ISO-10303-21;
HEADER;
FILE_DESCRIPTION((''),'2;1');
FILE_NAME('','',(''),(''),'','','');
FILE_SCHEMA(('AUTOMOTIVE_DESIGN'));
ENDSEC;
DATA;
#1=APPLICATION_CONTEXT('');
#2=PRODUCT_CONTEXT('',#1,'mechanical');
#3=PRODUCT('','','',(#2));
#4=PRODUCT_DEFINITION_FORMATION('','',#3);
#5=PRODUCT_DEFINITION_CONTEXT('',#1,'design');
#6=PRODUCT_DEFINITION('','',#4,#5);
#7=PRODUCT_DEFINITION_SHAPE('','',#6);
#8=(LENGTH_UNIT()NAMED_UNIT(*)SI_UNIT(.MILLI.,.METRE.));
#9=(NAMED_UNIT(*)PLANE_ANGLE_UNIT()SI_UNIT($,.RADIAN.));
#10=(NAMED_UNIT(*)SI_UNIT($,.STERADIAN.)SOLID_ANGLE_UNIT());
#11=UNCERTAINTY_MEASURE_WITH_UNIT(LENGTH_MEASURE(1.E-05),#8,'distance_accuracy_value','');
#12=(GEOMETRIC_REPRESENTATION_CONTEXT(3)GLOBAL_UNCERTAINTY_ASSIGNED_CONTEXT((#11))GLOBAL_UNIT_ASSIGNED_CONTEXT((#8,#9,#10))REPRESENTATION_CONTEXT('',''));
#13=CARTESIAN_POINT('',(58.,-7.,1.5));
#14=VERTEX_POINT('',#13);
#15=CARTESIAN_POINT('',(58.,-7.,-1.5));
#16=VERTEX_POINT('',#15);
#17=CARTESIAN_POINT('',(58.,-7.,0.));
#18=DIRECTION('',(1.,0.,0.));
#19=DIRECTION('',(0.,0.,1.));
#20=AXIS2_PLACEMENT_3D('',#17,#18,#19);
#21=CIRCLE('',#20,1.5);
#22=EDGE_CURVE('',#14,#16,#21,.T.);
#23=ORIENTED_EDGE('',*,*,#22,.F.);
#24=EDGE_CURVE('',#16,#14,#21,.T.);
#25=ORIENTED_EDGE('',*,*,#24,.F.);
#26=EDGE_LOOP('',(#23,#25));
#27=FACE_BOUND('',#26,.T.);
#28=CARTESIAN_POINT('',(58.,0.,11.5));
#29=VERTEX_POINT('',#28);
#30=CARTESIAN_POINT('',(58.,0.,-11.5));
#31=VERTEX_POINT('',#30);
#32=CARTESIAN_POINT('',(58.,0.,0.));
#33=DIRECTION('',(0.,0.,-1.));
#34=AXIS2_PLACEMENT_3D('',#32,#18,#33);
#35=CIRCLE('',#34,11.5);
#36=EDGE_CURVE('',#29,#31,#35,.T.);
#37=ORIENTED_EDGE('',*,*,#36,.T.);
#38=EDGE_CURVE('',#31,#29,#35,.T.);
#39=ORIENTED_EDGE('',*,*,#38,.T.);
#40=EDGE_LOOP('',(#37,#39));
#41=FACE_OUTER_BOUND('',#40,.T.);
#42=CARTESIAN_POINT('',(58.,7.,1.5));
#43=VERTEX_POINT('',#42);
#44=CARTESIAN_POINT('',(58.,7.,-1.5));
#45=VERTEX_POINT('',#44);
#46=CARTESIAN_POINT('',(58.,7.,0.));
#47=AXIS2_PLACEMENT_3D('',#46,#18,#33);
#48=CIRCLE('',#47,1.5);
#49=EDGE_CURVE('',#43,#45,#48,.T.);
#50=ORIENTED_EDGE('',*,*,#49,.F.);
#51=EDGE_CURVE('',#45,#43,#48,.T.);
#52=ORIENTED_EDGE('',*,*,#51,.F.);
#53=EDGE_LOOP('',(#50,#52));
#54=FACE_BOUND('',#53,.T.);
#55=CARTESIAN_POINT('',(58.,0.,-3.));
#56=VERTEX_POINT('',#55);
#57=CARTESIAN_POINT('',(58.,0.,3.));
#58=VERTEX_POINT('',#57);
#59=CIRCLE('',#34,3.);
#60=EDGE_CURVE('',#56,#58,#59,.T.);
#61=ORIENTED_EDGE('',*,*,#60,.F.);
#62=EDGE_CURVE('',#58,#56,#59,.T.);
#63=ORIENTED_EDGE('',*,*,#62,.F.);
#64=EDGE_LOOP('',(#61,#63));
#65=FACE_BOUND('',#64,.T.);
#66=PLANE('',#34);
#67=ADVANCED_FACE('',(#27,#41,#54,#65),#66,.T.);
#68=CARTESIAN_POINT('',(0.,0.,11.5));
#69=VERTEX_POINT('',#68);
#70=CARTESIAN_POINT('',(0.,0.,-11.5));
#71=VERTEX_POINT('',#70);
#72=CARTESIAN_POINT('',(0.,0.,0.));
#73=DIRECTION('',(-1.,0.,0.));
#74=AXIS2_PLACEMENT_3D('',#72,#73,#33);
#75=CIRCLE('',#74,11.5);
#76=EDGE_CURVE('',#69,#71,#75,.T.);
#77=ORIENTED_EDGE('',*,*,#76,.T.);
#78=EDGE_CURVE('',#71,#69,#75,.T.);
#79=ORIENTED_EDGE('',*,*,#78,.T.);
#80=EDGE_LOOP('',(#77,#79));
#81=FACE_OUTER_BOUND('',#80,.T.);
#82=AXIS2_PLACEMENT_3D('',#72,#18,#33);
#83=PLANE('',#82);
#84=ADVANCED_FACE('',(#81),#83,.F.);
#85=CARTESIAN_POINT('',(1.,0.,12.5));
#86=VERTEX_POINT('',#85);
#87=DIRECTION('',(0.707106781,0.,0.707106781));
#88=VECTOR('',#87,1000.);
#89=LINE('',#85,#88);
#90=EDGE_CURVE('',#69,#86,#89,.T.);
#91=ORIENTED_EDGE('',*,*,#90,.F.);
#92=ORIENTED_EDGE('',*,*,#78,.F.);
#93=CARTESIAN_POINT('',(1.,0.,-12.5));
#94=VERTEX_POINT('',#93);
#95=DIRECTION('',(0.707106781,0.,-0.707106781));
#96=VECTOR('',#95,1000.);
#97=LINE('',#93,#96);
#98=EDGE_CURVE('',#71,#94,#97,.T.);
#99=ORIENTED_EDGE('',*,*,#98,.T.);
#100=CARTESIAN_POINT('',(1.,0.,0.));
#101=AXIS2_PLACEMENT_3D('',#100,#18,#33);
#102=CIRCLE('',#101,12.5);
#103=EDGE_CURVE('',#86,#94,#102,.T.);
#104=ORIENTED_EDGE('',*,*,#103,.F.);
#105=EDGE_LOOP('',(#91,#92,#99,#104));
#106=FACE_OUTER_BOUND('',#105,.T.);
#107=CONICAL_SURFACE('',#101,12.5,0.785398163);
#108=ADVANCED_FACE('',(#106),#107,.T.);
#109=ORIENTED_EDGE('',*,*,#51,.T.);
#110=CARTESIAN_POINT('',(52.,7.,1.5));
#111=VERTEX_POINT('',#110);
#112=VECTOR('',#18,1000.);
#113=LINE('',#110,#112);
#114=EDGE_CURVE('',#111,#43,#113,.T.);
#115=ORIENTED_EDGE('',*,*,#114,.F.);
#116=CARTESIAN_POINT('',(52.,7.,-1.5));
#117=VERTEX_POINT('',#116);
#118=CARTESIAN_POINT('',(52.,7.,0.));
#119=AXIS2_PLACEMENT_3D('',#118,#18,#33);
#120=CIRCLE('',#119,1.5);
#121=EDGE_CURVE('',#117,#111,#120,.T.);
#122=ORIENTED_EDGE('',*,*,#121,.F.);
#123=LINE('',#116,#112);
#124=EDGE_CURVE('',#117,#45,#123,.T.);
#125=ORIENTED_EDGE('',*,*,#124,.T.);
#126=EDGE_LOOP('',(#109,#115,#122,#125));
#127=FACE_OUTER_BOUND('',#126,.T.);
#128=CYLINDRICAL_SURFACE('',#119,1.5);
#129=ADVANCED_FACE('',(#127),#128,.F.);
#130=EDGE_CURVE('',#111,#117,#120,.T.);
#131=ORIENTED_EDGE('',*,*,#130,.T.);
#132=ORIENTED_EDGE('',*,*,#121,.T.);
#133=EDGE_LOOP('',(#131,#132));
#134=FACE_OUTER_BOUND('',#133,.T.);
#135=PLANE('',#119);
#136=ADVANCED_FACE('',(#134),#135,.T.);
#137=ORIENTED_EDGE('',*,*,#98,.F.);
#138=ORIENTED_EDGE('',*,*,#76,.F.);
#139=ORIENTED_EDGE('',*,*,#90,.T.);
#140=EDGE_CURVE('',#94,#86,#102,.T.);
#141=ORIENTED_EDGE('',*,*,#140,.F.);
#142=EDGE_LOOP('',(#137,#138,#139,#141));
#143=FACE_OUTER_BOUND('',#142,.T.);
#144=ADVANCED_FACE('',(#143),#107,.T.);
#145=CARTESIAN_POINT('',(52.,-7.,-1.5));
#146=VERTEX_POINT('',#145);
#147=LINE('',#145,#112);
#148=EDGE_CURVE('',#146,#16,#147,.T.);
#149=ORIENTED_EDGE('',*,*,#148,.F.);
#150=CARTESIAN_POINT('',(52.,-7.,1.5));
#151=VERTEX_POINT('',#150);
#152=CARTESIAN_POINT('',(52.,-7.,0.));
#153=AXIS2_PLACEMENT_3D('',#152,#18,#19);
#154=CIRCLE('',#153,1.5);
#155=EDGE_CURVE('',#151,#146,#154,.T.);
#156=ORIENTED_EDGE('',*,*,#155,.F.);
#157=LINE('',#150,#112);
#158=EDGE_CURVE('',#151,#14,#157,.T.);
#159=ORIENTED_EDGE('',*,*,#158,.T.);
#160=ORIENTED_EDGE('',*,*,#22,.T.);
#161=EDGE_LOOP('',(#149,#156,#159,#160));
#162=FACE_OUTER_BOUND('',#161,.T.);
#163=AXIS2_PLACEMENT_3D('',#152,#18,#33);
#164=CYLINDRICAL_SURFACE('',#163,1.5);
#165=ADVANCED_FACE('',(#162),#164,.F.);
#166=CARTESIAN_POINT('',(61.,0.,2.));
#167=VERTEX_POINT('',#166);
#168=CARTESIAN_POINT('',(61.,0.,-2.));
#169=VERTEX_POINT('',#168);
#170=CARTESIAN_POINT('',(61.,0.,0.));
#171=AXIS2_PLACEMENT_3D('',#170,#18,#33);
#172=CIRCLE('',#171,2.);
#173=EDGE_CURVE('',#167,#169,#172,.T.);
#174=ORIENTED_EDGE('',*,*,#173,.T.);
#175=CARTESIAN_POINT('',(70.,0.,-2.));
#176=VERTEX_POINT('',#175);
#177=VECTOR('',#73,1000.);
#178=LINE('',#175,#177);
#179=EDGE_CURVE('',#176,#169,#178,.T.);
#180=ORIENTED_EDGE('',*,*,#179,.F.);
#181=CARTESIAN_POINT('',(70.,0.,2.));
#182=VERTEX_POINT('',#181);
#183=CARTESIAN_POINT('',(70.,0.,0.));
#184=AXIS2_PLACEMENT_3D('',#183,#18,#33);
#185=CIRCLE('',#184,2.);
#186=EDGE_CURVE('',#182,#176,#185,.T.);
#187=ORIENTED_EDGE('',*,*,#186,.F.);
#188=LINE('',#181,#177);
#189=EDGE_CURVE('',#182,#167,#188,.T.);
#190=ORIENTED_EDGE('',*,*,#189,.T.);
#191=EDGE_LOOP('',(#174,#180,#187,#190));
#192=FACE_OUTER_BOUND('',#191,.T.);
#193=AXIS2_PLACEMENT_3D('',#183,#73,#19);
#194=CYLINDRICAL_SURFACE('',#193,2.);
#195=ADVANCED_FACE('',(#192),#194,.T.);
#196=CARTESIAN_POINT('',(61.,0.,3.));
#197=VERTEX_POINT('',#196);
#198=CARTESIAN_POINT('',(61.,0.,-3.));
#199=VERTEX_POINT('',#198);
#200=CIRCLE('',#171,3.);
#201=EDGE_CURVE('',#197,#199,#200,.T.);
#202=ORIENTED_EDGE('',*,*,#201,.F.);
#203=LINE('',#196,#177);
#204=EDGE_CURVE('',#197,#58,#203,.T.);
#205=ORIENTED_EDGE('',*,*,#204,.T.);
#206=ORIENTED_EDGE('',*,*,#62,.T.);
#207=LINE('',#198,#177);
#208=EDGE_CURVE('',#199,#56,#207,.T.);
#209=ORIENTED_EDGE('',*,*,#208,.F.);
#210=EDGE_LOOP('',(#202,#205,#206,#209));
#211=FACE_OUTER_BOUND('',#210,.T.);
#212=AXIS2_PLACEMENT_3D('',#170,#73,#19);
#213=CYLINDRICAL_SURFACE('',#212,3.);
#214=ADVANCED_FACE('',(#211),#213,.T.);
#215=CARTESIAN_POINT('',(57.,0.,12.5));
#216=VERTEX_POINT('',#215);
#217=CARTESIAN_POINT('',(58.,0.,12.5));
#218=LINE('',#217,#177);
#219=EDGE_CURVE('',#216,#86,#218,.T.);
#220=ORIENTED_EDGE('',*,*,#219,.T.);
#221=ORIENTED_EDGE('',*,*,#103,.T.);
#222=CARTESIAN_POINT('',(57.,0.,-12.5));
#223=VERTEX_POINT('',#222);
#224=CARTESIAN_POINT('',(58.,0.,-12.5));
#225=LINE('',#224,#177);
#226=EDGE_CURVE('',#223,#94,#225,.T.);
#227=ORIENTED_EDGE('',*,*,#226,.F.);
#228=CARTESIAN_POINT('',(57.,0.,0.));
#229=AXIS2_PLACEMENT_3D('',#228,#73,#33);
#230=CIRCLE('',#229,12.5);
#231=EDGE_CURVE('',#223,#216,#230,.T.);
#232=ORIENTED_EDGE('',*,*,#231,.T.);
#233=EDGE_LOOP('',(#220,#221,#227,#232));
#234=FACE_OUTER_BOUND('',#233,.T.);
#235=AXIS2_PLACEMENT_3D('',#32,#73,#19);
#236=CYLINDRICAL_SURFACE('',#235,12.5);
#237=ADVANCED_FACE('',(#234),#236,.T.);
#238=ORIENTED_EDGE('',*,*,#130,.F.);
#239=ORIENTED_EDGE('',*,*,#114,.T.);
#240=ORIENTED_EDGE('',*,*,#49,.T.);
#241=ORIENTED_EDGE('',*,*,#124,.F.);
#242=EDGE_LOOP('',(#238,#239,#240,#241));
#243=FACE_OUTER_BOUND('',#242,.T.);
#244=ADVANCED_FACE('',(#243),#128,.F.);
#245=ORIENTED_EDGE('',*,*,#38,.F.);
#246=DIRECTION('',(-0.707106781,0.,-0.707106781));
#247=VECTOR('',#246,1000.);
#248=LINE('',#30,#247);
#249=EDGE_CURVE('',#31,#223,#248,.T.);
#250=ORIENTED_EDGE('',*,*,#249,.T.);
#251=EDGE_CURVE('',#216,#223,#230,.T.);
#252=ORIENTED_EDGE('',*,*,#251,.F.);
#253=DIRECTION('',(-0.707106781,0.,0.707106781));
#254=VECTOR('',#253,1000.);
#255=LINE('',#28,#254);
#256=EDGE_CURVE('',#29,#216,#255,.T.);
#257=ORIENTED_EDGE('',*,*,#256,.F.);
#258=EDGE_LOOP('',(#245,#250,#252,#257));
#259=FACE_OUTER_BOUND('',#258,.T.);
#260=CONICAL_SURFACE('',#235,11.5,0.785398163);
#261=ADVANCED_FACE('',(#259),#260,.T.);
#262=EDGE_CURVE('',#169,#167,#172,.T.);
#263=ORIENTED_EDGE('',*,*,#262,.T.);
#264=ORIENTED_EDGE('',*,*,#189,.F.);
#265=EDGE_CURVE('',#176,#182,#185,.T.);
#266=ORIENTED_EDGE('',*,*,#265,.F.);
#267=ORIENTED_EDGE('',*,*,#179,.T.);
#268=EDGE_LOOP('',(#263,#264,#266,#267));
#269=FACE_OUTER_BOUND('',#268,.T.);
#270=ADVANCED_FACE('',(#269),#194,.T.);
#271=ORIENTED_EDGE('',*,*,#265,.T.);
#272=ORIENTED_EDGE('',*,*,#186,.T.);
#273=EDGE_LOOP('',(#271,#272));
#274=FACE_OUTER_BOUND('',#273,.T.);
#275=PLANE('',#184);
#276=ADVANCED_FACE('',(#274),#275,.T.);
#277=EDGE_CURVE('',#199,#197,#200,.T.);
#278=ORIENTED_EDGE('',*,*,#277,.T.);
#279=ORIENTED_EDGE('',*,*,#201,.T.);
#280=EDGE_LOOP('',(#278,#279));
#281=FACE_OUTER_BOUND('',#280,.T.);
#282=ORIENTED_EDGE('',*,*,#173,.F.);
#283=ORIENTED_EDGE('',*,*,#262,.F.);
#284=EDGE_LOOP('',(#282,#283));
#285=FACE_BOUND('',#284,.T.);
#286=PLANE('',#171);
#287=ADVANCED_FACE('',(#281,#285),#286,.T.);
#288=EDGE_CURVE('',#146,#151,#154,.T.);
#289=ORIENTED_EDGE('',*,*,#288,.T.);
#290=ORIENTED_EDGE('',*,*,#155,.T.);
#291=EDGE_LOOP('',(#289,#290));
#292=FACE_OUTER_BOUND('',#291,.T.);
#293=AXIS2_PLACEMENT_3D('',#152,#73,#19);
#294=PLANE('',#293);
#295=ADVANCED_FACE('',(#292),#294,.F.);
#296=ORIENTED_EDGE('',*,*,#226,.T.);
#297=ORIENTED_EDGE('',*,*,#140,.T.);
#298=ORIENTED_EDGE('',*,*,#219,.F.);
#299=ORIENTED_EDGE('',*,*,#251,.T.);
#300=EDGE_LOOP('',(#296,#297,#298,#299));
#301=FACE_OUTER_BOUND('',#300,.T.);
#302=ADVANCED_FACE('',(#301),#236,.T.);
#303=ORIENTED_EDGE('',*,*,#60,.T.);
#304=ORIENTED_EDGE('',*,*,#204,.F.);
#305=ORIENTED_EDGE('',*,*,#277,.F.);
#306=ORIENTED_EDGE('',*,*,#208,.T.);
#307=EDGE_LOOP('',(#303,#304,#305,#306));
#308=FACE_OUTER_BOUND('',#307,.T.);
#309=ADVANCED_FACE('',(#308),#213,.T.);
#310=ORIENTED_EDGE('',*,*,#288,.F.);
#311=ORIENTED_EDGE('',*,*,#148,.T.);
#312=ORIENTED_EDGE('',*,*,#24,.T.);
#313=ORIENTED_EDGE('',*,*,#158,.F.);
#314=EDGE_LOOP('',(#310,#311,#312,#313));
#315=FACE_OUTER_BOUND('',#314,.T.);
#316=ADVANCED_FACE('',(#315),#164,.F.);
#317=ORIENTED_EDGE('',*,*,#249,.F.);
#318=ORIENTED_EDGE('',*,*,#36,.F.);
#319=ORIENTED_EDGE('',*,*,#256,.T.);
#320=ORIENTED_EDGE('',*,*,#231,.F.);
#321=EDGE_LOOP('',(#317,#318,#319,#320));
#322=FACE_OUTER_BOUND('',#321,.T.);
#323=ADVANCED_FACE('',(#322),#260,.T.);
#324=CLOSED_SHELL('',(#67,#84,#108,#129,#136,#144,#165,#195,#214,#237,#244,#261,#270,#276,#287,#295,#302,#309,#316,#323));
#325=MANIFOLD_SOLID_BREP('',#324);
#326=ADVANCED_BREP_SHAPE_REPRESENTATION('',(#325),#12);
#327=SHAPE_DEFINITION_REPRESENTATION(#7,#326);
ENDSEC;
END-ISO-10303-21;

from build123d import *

# Parameters (mm, degrees)
SKETCH1_R           = 12.5
BOSS_EXTRUDE1_DEPTH = 58
SKETCH2_R           = 3
BOSS_EXTRUDE2_DEPTH = 3
SKETCH3_R           = 2
BOSS_EXTRUDE3_DEPTH = 9
SKETCH4_R           = 1.5
CUT_EXTRUDE1_DEPTH  = 6
CHAMFER1_SIZE       = 1
CHAMFER2_SIZE       = 1


with BuildPart() as part:
    # Sketch1 → Boss-Extrude1 (new body)
    with BuildSketch(Plane(origin=(0, 0, 0), x_dir=(0, 0, -1), z_dir=(1, 0, 0))):
        with Locations(Location((0, 0, 0), (0, 0, 180))):
            Circle(SKETCH1_R)
    extrude(amount=BOSS_EXTRUDE1_DEPTH)

    # Sketch2 → Boss-Extrude2 (add)
    with BuildSketch(Plane(origin=(58, 0, 0), x_dir=(0, 0, -1), z_dir=(1, 0, 0))):
        Circle(SKETCH2_R)
    extrude(amount=BOSS_EXTRUDE2_DEPTH)

    # Sketch3 → Boss-Extrude3 (add)
    with BuildSketch(Plane(origin=(61, 0, 0), x_dir=(0, 0, -1), z_dir=(1, 0, 0))):
        Circle(SKETCH3_R)
    extrude(amount=BOSS_EXTRUDE3_DEPTH)

    # Sketch4 → Cut-Extrude1 (cut)
    with BuildSketch(Plane(origin=(58, 0, 0), x_dir=(0, 0, -1), z_dir=(1, 0, 0))):
        with Locations((0, 7)):
            Circle(SKETCH4_R)
        with Locations(Location((0, -7, 0), (0, 0, 180))):
            Circle(SKETCH4_R)
    extrude(amount=-CUT_EXTRUDE1_DEPTH, mode=Mode.SUBTRACT)

    # Chamfer1
    chamfer1_edges = [part.edges().sort_by_distance(p)[0] for p in [
        (58, 0, -12.5),
    ]]
    chamfer(chamfer1_edges, length=CHAMFER1_SIZE)

    # Chamfer2
    chamfer2_edges = [part.edges().sort_by_distance(p)[0] for p in [
        (0, 0, -12.5),
    ]]
    chamfer(chamfer2_edges, length=CHAMFER2_SIZE)


solid = part.part
